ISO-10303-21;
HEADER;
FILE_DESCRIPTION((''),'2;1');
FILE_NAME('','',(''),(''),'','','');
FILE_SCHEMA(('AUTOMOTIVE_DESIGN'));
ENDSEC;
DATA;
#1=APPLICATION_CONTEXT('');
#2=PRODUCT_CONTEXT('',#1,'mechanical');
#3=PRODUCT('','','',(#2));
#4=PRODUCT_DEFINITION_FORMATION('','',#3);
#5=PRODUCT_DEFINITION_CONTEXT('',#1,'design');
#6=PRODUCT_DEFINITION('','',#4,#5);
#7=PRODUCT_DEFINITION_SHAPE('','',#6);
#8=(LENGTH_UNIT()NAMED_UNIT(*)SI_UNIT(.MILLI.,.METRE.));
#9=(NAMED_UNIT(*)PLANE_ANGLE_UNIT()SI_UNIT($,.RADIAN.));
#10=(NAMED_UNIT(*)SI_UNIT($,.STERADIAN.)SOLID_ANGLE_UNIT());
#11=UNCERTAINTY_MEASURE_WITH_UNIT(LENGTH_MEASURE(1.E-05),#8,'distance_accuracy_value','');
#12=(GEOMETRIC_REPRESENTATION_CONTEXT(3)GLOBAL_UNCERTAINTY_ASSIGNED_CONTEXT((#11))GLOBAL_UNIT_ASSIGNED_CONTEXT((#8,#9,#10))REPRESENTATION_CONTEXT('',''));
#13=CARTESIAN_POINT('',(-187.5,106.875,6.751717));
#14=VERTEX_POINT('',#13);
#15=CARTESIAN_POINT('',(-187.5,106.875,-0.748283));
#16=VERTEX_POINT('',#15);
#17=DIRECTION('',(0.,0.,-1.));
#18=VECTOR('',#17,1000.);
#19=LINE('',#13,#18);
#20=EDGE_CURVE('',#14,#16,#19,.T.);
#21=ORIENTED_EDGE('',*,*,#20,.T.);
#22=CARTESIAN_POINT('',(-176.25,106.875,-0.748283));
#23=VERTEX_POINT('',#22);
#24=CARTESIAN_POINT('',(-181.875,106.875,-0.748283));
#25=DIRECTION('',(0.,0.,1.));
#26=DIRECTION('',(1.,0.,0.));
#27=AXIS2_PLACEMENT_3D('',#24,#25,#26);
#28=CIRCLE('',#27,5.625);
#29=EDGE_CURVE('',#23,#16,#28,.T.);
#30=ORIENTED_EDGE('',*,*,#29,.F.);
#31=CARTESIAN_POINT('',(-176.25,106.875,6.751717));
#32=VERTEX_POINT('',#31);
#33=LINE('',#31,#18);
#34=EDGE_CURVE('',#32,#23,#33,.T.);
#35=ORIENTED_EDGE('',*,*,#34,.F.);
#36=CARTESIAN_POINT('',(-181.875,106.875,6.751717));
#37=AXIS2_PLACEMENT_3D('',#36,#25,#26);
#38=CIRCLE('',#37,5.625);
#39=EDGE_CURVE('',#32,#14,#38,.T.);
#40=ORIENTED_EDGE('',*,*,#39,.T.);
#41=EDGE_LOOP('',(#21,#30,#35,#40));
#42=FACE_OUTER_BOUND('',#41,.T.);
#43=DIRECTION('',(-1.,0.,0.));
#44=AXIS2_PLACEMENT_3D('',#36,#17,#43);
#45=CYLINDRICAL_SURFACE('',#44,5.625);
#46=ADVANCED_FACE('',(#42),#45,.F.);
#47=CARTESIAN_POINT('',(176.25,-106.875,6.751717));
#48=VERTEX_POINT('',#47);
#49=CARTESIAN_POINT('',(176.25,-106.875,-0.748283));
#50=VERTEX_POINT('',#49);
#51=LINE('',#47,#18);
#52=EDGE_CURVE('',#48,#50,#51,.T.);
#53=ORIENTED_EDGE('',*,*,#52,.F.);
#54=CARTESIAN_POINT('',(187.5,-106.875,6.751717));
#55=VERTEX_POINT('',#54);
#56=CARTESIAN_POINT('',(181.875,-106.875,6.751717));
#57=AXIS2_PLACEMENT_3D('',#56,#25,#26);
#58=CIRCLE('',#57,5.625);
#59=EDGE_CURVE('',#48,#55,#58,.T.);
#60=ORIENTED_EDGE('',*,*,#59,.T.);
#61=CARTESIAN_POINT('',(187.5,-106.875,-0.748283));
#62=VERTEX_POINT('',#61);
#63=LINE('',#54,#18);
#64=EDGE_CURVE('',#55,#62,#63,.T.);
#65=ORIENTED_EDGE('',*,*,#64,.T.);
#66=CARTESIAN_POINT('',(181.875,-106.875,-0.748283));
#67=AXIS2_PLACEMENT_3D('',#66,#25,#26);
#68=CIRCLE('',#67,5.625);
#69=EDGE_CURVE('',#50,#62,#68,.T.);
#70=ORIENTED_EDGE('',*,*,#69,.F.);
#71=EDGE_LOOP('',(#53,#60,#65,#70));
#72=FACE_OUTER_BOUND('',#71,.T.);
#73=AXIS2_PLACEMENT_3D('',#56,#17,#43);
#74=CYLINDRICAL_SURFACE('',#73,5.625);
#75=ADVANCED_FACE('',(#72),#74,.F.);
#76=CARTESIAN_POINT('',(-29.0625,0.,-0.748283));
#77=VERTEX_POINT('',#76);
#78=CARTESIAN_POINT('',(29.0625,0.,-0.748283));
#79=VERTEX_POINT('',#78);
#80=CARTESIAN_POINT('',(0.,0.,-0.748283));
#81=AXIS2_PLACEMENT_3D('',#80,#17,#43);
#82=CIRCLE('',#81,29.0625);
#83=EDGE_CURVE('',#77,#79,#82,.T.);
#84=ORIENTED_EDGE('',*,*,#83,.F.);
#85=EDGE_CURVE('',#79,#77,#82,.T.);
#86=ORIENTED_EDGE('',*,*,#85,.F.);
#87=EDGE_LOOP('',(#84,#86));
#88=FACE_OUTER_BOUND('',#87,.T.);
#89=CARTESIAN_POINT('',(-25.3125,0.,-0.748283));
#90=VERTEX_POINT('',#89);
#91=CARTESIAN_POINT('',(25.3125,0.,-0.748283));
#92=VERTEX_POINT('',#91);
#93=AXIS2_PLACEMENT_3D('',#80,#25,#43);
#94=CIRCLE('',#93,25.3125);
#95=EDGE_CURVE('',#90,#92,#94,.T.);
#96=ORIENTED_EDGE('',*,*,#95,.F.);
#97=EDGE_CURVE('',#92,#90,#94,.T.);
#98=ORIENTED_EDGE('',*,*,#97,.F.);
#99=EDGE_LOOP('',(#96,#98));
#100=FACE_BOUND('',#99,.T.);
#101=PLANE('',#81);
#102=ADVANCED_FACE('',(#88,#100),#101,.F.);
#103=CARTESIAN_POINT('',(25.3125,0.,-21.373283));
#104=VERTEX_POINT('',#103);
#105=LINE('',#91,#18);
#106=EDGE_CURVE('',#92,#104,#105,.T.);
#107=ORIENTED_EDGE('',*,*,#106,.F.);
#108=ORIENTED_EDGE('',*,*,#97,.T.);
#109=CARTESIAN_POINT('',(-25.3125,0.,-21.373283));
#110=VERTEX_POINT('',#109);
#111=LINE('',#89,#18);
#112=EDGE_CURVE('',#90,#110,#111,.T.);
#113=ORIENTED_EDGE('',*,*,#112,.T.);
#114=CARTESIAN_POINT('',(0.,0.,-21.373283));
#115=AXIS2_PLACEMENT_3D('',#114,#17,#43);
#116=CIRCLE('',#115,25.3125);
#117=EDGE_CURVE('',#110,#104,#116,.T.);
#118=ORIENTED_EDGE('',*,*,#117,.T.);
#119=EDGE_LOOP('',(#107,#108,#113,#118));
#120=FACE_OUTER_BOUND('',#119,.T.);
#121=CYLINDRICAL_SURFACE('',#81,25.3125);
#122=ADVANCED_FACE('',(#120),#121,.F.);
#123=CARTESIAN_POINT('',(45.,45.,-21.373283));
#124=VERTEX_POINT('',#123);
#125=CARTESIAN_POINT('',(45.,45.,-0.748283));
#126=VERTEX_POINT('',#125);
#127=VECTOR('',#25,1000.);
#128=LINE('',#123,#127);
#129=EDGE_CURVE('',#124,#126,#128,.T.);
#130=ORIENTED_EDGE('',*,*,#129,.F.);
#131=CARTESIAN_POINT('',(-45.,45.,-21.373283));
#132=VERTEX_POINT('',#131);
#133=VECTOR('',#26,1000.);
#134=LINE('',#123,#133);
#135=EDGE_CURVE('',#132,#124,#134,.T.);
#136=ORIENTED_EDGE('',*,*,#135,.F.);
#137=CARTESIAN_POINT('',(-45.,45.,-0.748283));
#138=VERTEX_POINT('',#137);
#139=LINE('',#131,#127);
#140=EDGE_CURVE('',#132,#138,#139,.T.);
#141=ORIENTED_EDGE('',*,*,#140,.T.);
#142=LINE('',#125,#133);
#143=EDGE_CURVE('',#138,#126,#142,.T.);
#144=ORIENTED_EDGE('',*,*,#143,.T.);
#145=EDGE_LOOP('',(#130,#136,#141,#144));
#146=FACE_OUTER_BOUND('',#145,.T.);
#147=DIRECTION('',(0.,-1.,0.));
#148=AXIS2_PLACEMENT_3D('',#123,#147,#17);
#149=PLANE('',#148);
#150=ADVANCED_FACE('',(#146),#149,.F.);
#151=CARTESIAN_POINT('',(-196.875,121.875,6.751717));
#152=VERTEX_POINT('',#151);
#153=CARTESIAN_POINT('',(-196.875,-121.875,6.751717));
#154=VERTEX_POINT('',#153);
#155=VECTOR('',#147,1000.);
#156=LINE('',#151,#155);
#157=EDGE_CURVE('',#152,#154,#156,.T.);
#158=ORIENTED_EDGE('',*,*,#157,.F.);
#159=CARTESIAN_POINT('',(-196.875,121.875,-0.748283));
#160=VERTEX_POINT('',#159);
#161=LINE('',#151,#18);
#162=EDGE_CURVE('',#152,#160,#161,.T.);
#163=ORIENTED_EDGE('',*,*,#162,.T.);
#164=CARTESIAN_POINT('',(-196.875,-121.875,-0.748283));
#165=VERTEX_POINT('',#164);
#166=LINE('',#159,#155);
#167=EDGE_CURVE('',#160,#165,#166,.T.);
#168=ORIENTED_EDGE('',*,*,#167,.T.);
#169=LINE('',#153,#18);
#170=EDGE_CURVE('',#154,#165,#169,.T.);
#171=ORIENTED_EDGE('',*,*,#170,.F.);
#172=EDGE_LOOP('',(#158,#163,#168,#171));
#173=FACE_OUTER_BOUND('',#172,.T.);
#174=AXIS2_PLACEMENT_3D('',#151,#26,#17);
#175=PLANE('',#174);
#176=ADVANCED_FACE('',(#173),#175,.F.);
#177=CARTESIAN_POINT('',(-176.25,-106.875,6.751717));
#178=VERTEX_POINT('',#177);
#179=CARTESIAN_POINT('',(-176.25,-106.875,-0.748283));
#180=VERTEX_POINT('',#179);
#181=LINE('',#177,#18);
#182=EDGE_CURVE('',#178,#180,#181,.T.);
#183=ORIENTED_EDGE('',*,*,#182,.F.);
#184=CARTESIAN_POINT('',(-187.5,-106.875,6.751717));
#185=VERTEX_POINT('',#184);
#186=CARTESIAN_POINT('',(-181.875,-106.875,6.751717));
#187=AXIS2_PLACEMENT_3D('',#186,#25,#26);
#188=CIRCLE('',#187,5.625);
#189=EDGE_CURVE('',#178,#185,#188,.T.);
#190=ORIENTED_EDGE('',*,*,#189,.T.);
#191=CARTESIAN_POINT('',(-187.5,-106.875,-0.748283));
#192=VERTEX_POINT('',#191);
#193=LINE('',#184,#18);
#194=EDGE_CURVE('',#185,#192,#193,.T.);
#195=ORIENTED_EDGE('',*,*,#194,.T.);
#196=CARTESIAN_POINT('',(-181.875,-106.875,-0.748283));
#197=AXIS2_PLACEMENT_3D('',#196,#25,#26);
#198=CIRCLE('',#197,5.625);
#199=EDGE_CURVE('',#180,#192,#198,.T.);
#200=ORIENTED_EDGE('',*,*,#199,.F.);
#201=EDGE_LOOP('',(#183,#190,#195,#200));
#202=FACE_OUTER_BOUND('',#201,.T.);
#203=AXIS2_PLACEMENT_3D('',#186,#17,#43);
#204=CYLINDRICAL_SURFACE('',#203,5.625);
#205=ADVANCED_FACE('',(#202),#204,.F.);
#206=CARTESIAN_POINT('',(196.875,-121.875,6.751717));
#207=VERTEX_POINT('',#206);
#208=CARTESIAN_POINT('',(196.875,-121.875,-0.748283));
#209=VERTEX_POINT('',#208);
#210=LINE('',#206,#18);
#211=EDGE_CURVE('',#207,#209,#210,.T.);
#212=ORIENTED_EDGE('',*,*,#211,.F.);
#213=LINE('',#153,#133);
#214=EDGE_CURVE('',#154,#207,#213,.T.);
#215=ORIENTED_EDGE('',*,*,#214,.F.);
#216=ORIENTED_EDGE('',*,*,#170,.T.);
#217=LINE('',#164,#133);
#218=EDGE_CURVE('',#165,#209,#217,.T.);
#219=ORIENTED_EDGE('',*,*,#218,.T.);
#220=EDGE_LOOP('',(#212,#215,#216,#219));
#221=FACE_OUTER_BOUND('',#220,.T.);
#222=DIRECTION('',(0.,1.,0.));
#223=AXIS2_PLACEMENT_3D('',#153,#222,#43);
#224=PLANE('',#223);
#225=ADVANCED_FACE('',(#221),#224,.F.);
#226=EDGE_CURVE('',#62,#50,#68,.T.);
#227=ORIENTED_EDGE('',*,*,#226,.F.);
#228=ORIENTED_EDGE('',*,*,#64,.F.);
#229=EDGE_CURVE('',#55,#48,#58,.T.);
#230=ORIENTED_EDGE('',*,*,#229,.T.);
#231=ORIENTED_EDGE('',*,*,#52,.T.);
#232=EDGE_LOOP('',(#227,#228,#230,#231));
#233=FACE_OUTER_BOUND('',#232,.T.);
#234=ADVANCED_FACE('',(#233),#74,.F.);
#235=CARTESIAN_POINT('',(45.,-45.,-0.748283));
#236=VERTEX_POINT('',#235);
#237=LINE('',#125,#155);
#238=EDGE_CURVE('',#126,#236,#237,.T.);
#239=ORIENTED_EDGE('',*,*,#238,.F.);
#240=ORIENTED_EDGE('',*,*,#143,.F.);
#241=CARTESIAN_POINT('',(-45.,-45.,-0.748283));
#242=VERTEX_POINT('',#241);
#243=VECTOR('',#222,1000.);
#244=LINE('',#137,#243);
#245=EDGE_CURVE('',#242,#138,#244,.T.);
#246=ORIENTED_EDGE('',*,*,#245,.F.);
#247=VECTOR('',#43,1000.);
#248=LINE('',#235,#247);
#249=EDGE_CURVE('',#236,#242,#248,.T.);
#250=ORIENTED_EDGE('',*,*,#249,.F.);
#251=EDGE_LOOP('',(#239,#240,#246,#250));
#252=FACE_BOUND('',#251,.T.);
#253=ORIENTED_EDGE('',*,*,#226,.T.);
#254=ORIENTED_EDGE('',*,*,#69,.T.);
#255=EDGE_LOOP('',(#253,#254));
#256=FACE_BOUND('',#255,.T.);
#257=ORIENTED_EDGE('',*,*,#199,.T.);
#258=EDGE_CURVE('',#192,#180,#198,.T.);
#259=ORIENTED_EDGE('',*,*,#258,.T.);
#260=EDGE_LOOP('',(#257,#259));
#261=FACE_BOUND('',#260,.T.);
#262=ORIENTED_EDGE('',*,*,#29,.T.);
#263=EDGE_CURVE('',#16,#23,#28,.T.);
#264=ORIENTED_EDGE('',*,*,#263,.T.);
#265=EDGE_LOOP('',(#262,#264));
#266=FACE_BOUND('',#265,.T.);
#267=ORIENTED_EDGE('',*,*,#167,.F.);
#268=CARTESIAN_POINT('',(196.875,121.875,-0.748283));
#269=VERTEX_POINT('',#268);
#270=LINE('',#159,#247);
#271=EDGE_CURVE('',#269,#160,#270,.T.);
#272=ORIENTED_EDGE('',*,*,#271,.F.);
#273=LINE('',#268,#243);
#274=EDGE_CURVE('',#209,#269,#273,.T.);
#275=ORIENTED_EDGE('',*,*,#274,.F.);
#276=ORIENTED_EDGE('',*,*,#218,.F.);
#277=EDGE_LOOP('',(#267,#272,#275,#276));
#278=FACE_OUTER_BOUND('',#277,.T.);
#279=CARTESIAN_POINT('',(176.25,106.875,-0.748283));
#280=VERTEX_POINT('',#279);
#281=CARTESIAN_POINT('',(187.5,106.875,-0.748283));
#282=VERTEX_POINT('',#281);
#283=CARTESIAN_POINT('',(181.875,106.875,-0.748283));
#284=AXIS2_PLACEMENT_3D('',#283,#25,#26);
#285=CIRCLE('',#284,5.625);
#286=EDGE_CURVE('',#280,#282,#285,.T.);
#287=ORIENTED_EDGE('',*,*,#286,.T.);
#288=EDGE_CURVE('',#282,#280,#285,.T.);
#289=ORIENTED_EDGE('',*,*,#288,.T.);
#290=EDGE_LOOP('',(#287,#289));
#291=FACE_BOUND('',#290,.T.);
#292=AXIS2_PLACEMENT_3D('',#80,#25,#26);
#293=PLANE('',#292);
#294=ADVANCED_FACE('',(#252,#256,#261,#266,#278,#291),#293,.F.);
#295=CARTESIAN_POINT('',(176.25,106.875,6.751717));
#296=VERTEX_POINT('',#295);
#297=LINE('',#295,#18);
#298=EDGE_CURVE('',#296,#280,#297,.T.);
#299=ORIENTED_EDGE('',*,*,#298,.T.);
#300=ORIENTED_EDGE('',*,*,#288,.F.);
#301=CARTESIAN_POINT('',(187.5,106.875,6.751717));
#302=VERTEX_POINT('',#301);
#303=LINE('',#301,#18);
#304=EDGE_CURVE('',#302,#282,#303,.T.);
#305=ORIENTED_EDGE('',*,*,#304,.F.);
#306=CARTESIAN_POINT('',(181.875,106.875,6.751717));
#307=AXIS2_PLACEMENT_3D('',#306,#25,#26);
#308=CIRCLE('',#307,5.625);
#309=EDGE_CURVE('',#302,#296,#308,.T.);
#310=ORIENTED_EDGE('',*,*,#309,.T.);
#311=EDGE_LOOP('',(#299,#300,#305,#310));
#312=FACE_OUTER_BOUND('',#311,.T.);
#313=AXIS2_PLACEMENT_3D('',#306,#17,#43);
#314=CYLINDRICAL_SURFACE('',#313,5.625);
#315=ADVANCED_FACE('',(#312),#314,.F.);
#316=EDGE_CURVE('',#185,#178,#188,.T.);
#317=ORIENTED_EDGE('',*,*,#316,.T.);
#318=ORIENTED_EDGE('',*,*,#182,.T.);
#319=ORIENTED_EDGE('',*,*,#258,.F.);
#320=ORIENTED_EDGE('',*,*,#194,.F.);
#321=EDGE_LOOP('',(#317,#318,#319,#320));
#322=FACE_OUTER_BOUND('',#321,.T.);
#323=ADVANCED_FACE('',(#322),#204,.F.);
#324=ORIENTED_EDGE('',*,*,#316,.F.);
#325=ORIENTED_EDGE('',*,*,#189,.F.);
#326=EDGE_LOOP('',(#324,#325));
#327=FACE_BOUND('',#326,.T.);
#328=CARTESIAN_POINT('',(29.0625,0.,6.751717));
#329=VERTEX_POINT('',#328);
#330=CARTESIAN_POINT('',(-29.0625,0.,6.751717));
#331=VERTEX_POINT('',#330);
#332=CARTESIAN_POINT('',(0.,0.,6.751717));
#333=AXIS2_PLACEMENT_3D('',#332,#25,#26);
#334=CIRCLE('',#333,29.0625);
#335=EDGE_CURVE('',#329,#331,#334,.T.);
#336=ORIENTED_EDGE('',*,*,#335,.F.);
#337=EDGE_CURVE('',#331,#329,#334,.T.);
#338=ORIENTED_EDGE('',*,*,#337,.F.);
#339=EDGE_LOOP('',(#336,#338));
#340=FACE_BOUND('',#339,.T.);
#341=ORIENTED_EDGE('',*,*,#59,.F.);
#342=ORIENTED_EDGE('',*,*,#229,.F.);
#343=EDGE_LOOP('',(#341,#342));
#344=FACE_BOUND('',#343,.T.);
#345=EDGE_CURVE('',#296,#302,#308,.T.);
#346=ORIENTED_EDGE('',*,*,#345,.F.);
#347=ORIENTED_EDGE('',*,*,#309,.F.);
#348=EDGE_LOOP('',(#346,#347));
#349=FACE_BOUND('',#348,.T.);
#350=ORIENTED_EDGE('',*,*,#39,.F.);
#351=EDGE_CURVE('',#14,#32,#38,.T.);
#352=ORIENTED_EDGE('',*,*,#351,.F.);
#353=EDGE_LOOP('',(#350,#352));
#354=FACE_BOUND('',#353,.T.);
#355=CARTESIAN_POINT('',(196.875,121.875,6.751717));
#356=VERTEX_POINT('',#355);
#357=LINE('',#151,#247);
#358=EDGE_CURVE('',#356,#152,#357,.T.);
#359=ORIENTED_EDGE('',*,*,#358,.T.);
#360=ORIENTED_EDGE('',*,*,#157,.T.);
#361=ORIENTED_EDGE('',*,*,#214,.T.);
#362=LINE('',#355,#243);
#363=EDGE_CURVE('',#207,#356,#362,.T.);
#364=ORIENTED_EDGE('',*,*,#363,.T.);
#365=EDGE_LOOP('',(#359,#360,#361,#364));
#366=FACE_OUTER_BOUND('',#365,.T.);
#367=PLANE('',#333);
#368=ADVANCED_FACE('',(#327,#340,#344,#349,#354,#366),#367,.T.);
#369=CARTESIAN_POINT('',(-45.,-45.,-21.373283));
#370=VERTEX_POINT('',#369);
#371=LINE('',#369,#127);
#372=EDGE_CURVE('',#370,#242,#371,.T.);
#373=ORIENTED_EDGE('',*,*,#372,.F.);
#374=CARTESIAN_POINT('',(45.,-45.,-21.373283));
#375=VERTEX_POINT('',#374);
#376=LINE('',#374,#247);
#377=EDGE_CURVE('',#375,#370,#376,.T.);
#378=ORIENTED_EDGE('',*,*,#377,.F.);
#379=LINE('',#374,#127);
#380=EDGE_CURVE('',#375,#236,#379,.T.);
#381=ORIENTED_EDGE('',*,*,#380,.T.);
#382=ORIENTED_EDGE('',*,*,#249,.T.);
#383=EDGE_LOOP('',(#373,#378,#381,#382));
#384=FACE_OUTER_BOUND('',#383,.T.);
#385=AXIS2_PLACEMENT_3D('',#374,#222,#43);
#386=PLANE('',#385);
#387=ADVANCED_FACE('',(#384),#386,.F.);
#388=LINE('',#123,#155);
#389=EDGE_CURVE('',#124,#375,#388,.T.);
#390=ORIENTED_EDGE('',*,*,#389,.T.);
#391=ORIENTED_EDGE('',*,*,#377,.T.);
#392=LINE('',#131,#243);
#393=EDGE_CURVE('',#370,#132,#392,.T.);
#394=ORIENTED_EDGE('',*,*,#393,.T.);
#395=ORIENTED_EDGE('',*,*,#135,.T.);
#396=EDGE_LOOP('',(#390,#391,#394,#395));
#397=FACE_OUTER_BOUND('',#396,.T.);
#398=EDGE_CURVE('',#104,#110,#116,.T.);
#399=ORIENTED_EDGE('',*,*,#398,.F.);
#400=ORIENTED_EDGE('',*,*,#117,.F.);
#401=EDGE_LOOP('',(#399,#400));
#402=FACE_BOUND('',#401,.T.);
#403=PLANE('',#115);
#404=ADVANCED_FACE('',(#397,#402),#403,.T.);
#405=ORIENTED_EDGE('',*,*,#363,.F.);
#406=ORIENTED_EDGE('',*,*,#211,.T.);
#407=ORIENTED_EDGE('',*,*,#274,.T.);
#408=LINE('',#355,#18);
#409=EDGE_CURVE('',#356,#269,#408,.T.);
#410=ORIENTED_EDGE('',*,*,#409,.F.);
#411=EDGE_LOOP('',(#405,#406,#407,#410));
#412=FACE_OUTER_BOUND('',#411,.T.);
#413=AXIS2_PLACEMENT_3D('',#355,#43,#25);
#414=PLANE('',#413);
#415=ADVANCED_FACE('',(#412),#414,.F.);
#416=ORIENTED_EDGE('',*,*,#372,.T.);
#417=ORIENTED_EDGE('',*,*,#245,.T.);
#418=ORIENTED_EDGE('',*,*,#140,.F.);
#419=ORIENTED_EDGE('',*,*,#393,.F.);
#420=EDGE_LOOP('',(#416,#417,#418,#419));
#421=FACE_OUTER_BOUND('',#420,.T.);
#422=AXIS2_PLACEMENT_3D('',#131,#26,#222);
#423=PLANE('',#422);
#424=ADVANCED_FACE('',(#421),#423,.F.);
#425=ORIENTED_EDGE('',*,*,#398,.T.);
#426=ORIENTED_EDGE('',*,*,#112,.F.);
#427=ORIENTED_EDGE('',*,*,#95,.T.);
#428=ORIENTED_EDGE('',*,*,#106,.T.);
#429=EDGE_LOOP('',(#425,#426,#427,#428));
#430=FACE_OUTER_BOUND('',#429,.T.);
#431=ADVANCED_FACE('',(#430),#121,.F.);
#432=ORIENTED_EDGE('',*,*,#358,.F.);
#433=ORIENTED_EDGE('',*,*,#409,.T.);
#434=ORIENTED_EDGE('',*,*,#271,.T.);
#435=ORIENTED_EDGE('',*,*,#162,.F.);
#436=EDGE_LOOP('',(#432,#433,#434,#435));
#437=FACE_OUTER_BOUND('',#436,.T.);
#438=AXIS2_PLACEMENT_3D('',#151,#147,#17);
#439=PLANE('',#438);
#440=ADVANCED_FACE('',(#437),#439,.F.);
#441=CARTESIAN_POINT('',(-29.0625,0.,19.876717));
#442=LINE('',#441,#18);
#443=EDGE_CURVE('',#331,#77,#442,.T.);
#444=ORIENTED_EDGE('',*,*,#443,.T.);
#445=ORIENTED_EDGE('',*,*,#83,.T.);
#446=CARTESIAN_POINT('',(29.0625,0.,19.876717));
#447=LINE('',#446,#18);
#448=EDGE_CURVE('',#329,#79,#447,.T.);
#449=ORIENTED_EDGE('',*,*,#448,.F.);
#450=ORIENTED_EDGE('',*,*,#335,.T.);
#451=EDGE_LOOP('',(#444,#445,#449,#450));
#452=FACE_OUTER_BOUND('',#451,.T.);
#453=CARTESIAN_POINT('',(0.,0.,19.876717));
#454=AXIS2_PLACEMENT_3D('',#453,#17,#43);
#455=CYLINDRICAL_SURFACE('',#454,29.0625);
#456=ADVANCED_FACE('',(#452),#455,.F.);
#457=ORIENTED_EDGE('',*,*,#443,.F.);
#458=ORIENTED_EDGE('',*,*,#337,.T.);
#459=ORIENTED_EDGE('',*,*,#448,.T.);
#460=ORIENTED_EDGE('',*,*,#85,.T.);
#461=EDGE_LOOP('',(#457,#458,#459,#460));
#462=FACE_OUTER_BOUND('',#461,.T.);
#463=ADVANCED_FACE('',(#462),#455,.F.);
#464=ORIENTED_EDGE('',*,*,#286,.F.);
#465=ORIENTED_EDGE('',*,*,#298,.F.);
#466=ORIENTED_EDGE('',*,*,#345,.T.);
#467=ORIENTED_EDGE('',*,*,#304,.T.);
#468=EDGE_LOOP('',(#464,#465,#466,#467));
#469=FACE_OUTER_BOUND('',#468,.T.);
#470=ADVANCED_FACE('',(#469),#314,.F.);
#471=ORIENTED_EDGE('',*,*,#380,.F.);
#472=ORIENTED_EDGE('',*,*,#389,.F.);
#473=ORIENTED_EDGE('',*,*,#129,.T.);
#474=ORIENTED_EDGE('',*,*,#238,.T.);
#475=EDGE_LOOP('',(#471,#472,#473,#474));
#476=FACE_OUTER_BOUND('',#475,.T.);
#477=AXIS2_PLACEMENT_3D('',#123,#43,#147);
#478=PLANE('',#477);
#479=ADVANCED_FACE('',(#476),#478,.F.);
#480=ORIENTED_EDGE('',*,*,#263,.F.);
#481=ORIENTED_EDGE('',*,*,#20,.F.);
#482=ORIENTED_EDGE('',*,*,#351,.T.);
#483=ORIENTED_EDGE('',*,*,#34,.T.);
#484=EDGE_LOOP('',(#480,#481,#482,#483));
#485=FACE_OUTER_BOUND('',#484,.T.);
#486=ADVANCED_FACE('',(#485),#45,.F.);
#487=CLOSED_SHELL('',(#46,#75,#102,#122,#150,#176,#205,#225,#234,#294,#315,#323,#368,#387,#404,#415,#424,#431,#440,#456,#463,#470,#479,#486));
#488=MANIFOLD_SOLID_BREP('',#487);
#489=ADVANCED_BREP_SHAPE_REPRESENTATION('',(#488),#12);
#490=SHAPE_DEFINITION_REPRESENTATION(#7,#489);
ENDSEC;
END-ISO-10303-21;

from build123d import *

# Parameters (mm, degrees)
SKETCH1_W           = 210
SKETCH1_H           = 130
SKETCH1_R           = 3
BOSS_EXTRUDE1_DEPTH = 4
SKETCH2_W           = 48
SKETCH2_H           = 48
BOSS_EXTRUDE2_DEPTH = 11
SKETCH3_R           = 13.5
CUT_EXTRUDE1_DEPTH  = 11
SKETCH4_R           = 15.5
CUT_EXTRUDE2_DEPTH  = 11
SCALE_1_SCALE       = 1.875


with BuildPart() as part:
    # Sketch1 → Boss-Extrude1 (new body)
    with BuildSketch(Plane.XY):
        Rectangle(SKETCH1_W, SKETCH1_H)
        with Locations((97, 57)):
            Circle(SKETCH1_R, mode=Mode.SUBTRACT)
        with Locations((-97, 57)):
            Circle(SKETCH1_R, mode=Mode.SUBTRACT)
        with Locations((-97, -57)):
            Circle(SKETCH1_R, mode=Mode.SUBTRACT)
        with Locations((97, -57)):
            Circle(SKETCH1_R, mode=Mode.SUBTRACT)
    extrude(amount=BOSS_EXTRUDE1_DEPTH)

    # Sketch2 → Boss-Extrude2 (add)
    with BuildSketch(Plane(origin=(0, 0, 0), x_dir=(-1, 0, 0), z_dir=(0, 0, -1))):
        Rectangle(SKETCH2_W, SKETCH2_H)
    extrude(amount=BOSS_EXTRUDE2_DEPTH)

    # Sketch3 → Cut-Extrude1 (cut)
    with BuildSketch(Plane(origin=(0, 0, -11), x_dir=(-1, 0, 0), z_dir=(0, 0, -1))):
        Circle(SKETCH3_R)
    extrude(amount=-CUT_EXTRUDE1_DEPTH, mode=Mode.SUBTRACT)

    # Sketch4 → Cut-Extrude2 (cut)
    with BuildSketch(Plane(origin=(0, 0, 0), x_dir=(-1, 0, 0), z_dir=(0, 0, -1))):
        Circle(SKETCH4_R)
    extrude(amount=-CUT_EXTRUDE2_DEPTH, mode=Mode.SUBTRACT)


with BuildPart() as part_1:
    # Scale 1: scaled about (0, 0, 0.855180598)
    add(part.part.scale(SCALE_1_SCALE).moved(Location((0, 0, -0.748283023))))


solid = part_1.part
